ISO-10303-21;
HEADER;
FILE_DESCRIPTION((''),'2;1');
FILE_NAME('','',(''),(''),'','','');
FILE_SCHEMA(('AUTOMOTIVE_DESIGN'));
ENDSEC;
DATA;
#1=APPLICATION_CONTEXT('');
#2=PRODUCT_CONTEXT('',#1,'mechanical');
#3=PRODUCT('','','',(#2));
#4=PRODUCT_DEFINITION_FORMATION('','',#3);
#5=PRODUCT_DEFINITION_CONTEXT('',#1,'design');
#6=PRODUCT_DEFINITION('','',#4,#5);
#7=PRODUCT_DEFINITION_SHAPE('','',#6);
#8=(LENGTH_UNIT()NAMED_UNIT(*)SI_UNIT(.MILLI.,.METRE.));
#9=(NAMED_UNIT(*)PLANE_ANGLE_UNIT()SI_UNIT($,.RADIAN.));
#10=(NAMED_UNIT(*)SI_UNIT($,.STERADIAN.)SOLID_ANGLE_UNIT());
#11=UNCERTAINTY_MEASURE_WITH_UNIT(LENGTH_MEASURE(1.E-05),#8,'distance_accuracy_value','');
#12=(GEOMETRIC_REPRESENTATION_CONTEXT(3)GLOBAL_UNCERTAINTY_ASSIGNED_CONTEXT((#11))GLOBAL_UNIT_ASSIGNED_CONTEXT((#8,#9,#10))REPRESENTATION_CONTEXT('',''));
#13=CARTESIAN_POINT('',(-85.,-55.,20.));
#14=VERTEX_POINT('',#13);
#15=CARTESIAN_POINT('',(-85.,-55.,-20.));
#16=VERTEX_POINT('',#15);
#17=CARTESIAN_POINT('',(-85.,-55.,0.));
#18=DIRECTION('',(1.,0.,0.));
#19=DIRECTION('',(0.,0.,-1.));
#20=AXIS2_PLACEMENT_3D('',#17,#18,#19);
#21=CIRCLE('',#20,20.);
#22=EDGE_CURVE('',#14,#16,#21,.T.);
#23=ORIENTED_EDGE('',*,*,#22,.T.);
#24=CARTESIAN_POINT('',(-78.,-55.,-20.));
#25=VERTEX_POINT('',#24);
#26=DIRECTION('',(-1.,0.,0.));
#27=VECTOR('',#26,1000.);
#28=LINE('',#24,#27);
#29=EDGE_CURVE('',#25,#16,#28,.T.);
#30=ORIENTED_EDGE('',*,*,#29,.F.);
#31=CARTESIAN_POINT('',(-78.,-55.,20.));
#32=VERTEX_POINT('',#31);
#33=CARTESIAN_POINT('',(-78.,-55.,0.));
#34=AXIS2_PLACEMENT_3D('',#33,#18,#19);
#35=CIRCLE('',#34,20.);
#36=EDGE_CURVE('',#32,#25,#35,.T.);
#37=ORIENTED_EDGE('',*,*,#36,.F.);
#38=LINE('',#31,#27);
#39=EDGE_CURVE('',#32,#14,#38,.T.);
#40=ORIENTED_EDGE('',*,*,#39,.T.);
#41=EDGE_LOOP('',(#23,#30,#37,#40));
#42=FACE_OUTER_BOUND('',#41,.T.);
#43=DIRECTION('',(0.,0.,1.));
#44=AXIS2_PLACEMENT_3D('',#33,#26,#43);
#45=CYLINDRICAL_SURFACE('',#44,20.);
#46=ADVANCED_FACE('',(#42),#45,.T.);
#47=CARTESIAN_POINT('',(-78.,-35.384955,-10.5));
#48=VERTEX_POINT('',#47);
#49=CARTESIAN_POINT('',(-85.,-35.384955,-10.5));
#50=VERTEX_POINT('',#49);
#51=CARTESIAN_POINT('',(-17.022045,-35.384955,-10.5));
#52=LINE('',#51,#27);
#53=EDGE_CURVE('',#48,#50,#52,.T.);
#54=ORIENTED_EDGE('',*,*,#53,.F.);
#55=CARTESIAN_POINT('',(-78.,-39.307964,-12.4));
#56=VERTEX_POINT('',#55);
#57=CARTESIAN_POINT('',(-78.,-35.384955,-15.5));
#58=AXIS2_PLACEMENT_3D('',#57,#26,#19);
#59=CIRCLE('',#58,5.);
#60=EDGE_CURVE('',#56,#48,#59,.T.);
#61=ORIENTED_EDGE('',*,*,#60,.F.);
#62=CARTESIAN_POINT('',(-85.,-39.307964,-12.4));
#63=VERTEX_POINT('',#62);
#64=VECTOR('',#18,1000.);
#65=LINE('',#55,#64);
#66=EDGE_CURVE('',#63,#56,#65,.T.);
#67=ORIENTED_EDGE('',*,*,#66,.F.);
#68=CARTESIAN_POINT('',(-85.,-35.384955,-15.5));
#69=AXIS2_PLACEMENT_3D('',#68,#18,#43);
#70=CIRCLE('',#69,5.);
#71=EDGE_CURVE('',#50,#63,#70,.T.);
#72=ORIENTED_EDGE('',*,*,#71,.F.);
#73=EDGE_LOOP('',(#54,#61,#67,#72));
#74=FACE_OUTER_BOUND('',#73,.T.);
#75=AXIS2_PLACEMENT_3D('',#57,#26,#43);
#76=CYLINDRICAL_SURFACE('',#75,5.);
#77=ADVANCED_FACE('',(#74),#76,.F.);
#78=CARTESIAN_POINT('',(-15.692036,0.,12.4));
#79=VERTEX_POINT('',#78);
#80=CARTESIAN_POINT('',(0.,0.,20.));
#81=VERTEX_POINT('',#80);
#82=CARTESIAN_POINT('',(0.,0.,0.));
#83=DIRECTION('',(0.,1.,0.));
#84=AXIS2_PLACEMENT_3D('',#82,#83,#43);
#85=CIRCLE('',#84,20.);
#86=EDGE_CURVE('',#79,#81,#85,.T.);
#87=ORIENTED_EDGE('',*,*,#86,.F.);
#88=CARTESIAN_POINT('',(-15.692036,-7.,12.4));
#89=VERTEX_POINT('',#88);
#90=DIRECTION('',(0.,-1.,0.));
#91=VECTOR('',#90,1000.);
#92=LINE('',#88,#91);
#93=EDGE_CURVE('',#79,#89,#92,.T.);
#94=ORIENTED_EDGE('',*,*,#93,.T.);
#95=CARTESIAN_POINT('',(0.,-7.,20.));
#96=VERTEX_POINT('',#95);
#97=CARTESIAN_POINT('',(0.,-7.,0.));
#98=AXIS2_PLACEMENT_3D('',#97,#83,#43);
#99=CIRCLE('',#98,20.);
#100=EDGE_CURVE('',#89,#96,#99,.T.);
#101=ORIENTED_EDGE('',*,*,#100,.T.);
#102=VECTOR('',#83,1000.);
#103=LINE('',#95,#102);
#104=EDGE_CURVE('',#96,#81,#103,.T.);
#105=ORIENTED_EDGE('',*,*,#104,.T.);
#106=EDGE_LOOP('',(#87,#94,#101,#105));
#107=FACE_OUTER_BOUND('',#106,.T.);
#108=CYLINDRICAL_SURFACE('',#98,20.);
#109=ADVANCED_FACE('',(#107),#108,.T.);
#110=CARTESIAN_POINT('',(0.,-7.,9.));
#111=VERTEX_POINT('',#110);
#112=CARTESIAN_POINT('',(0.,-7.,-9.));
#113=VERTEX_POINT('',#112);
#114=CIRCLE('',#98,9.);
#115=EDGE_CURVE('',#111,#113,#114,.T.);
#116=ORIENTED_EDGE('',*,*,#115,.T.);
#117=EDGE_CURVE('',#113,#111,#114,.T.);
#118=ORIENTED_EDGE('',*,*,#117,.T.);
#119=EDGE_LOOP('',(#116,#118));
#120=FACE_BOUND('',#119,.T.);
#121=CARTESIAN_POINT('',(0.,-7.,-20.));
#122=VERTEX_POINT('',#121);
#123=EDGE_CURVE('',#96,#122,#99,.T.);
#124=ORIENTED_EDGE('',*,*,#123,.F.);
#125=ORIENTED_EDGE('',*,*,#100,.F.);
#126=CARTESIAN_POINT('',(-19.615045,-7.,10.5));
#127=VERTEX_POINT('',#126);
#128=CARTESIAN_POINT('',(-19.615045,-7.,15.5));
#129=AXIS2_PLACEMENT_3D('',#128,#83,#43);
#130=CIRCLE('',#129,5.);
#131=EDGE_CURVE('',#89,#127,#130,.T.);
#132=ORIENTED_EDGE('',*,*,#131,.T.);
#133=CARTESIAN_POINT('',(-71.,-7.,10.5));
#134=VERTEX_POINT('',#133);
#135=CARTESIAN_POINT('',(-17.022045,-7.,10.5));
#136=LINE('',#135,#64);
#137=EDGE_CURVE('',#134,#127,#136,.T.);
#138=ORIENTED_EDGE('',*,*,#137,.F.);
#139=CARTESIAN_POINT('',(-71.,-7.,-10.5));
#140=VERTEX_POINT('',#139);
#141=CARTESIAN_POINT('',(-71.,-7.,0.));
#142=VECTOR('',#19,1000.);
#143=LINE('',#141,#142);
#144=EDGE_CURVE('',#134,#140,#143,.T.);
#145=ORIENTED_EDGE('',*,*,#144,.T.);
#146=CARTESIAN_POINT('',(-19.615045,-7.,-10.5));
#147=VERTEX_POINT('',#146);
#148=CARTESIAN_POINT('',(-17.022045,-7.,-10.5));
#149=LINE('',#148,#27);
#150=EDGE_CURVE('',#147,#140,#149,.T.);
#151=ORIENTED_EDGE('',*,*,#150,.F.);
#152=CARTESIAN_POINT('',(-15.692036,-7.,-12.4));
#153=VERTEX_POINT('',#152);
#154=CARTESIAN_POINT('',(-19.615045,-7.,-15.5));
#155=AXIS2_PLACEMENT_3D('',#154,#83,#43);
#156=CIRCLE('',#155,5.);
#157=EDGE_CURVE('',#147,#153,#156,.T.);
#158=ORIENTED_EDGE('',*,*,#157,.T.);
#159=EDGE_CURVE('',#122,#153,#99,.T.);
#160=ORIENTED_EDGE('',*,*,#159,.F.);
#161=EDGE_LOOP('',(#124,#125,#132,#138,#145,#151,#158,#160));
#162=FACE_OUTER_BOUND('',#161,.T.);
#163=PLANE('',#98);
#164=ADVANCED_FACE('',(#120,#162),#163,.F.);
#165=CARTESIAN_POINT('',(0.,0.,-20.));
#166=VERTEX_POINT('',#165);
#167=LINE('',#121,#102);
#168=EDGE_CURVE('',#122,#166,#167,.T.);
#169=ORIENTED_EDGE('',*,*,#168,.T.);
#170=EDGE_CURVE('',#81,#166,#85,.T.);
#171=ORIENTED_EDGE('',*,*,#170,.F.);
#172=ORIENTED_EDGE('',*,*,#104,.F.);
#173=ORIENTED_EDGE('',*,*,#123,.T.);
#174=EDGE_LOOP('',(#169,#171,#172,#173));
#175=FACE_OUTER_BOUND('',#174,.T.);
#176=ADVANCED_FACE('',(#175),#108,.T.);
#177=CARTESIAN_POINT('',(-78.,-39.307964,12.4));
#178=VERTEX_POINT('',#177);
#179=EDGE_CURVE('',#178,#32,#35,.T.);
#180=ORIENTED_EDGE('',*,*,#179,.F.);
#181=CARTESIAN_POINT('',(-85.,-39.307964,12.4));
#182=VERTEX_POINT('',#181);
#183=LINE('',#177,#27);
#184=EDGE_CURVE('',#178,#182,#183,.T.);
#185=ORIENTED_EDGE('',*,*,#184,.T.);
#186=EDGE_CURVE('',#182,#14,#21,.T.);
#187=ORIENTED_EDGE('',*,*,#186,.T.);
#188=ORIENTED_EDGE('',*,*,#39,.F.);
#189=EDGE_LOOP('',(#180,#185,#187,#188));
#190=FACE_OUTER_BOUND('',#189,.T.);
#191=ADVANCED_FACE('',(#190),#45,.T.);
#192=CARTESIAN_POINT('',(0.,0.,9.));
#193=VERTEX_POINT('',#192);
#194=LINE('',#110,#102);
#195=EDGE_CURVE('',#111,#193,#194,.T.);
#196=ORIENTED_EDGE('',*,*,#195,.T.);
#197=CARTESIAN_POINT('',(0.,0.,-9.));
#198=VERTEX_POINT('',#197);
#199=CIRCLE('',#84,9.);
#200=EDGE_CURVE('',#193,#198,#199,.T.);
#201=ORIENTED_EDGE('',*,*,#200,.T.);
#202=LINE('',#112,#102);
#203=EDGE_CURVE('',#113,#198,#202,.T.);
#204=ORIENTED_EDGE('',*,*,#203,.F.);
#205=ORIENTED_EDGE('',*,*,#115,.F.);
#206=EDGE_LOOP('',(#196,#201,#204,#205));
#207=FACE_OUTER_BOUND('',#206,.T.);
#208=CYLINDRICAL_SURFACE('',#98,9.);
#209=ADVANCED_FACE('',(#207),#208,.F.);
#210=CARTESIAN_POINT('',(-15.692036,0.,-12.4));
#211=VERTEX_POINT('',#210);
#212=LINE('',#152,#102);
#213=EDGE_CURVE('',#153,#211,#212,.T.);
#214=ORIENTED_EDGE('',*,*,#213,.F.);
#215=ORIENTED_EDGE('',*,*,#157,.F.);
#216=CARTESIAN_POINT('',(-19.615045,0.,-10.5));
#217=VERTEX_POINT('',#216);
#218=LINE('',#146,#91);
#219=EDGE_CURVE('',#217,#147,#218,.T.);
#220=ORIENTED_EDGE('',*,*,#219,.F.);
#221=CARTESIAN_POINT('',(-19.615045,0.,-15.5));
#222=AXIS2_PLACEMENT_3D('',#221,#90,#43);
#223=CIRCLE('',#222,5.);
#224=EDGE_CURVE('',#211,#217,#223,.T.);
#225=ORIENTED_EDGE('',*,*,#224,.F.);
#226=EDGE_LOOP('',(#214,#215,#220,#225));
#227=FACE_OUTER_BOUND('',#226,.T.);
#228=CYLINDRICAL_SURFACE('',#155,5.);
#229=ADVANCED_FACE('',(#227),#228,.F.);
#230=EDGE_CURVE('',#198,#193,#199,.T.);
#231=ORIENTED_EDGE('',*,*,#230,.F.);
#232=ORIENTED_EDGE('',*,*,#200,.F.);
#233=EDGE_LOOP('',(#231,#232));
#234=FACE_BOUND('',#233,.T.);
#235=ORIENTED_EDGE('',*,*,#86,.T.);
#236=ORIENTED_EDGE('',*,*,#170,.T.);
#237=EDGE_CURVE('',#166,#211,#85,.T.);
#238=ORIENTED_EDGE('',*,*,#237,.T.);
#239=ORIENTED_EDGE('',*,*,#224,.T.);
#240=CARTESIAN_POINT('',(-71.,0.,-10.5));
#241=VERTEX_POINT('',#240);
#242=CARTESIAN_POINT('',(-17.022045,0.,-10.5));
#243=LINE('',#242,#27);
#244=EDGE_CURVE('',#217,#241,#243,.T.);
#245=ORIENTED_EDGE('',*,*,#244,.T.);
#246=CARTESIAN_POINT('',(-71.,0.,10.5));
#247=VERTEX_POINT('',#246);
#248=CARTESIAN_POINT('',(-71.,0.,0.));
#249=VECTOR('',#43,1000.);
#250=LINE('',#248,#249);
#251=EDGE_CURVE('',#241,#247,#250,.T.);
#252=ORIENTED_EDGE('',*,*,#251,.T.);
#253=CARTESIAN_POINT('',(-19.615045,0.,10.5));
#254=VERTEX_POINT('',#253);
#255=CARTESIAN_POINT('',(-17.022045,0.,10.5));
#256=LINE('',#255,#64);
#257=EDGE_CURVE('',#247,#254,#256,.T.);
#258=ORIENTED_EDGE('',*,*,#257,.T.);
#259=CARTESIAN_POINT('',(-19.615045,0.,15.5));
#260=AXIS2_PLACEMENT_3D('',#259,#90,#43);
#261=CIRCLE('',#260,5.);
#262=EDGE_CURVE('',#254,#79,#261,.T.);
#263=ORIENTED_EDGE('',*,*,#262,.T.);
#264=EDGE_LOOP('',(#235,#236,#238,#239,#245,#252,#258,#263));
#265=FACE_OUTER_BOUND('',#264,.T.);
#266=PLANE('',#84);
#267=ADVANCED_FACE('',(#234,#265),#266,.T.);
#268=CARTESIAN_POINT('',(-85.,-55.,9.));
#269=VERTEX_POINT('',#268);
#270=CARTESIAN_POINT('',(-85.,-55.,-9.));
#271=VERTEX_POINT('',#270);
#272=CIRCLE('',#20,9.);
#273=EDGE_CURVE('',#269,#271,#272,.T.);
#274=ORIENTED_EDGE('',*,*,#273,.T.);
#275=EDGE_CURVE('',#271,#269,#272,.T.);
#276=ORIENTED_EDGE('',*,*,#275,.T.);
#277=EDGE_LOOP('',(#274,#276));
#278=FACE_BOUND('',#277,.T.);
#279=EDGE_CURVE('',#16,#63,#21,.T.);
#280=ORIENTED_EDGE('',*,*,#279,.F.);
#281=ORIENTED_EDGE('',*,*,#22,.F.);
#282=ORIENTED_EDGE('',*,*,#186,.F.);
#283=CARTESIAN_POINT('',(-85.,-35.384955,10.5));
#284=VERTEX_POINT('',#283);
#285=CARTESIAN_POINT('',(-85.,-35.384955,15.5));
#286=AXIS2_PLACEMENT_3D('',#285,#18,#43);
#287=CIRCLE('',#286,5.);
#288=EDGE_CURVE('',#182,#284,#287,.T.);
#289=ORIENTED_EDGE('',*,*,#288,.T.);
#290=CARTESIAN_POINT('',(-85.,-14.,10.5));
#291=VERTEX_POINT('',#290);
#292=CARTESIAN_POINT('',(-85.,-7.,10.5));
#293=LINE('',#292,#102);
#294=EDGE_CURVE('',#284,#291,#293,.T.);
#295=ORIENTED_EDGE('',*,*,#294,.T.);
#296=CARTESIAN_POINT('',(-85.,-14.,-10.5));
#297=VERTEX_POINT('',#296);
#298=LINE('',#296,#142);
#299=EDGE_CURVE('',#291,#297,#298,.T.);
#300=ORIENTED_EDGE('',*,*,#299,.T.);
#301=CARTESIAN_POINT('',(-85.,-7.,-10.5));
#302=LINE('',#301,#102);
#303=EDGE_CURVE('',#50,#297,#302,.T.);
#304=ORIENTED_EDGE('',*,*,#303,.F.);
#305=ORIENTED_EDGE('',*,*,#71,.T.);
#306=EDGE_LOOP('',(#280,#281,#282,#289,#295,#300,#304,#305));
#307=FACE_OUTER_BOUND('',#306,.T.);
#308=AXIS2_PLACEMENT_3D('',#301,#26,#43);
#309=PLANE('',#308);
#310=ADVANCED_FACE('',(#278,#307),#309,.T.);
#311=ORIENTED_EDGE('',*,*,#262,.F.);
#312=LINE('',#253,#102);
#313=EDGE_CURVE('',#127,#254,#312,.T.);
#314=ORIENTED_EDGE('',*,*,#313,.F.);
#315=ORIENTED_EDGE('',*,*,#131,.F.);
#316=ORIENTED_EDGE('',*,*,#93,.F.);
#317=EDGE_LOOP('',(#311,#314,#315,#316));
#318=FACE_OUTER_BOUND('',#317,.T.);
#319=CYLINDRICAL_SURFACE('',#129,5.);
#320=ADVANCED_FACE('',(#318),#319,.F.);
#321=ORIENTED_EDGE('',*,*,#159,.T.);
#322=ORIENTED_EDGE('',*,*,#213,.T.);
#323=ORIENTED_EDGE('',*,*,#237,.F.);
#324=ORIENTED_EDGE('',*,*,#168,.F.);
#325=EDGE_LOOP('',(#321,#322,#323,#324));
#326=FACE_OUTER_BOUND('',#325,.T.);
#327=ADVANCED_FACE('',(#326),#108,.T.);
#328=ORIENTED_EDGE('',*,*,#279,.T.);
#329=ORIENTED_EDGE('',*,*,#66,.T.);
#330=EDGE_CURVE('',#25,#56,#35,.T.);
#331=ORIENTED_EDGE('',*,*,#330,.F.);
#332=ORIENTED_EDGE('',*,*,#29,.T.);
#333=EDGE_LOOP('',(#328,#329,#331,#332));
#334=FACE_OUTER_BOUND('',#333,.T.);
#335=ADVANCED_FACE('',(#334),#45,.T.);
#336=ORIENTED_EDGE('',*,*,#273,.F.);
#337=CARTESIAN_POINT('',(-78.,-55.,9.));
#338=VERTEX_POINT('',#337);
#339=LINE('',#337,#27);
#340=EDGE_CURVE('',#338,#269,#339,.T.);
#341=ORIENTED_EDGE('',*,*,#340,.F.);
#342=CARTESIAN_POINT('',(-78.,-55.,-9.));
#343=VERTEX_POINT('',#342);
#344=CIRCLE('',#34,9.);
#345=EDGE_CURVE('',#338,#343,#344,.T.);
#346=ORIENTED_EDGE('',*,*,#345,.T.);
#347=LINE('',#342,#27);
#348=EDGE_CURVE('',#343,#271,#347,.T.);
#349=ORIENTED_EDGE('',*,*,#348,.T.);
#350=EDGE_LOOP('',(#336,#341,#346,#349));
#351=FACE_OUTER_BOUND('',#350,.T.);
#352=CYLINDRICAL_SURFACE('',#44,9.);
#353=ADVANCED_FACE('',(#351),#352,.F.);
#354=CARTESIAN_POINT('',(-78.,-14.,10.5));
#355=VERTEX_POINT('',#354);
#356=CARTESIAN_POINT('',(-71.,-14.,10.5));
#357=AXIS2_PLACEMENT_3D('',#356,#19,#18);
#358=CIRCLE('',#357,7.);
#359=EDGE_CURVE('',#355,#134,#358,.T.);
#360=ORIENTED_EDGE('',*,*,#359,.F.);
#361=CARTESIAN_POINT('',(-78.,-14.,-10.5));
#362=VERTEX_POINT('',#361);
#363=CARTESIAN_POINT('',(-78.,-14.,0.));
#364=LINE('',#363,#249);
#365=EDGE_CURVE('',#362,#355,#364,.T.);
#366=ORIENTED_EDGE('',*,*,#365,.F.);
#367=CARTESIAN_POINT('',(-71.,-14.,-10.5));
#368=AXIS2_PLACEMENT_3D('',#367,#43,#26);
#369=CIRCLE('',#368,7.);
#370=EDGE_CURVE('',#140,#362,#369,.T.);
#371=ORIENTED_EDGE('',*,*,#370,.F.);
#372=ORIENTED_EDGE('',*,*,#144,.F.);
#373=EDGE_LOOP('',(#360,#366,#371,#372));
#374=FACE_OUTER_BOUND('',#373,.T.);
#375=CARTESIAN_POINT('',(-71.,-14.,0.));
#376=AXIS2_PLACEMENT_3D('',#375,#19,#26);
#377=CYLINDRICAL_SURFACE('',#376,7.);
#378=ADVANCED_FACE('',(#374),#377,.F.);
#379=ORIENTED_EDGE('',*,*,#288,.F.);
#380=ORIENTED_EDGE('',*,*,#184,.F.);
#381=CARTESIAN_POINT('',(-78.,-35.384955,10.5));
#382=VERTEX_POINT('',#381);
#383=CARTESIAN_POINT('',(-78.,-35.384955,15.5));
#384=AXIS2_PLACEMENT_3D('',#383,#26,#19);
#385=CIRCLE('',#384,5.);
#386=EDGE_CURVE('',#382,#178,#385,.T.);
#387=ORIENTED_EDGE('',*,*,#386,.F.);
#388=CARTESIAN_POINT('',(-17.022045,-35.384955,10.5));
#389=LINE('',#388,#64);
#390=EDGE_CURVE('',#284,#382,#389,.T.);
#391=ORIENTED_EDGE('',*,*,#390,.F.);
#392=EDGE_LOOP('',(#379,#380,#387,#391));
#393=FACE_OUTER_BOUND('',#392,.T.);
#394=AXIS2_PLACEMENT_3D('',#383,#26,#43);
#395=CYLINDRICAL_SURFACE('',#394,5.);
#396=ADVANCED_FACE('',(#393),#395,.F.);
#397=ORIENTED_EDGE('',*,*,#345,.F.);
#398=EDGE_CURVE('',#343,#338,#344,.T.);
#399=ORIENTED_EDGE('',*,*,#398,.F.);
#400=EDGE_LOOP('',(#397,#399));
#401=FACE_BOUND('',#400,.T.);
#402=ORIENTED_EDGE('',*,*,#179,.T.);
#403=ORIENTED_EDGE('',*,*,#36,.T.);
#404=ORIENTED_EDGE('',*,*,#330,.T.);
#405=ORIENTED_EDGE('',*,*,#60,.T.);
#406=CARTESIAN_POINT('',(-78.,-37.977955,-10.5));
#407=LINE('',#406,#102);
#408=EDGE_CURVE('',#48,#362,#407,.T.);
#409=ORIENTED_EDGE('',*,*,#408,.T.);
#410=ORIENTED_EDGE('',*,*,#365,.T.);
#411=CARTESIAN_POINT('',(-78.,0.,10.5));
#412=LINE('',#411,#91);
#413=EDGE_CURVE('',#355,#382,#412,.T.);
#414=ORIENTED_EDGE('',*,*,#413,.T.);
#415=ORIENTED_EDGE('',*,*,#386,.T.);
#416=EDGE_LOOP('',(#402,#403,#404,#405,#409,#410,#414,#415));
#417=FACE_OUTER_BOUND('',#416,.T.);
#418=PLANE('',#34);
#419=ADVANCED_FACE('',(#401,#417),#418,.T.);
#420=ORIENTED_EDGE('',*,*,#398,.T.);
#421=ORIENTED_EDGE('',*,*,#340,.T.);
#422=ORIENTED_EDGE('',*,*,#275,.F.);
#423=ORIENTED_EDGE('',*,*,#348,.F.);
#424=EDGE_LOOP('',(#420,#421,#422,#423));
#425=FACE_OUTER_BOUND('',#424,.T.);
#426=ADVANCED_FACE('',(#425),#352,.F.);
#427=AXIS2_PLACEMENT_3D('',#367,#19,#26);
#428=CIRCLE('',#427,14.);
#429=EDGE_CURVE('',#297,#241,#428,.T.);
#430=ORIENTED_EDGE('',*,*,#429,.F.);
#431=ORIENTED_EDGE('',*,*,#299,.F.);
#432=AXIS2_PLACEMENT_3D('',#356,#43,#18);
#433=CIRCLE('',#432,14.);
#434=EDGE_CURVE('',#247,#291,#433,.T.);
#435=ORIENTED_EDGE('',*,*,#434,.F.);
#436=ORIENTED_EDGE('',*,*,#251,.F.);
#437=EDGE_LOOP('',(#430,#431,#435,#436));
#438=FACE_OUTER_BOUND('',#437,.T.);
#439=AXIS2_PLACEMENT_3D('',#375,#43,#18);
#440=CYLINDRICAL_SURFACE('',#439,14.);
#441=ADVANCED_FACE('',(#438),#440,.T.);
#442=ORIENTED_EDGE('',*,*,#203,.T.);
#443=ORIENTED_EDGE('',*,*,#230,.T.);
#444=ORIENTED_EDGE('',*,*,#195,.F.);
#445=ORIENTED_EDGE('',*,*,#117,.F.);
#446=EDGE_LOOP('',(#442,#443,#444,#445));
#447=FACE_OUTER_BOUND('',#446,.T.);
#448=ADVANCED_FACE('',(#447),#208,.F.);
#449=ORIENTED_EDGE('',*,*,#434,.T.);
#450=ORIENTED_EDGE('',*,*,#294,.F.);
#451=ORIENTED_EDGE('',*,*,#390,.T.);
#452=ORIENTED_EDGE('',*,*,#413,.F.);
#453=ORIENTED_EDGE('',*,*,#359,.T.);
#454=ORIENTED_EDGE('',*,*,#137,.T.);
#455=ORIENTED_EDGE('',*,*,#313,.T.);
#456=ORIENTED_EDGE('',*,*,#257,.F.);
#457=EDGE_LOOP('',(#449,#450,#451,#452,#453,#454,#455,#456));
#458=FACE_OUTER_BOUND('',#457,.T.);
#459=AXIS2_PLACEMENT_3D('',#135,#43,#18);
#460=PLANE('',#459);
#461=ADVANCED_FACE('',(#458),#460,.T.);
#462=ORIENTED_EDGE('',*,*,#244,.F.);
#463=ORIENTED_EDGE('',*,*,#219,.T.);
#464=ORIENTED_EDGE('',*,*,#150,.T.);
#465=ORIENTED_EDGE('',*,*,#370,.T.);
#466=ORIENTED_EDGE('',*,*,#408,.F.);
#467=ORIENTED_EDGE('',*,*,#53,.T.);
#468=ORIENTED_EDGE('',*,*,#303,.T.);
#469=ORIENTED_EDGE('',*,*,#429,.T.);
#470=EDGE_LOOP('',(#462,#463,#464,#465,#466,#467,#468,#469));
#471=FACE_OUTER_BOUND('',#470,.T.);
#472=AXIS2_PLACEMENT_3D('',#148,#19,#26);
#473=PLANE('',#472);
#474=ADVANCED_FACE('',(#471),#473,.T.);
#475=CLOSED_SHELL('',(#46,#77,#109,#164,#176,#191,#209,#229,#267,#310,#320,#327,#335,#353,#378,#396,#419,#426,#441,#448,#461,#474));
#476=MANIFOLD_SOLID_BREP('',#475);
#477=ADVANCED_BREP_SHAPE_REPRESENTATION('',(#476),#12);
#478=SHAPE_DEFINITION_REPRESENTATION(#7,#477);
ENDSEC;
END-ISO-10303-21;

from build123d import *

# Parameters (mm, degrees)
HORIZONTAL_ARM_PROFILE_R    = 9
HORIZONTAL_ARM_7MM_DEPTH    = 7
VERTICAL_ARM_PROFILE_R      = 9
VERTICAL_ARM_7MM_DEPTH      = 7
BEND_FILLET_R5_R            = 5
HORIZONTAL_ARM_FILLET_R14_R = 14
BEND_FILLET_R7_R            = 7


with BuildPart() as part:
    # Horizontal Arm Profile → Horizontal Arm 7mm (new body)
    with BuildSketch(Plane(origin=(0, 0, 0), x_dir=(1, 0, 0), z_dir=(0, 1, 0))):
        with BuildLine():
            Line((-17.022044531, 10.5), (-85, 10.5))
            Line((-85, 10.5), (-85, -10.5))
            Line((-85, -10.5), (-17.022044531, -10.5))
            ThreePointArc((-17.022044531, -10.5), (20, 0), (-17.022044531, 10.5))
        make_face()
        with Locations(Location((0, 0, 0), (0, 0, 270))):
            Circle(HORIZONTAL_ARM_PROFILE_R, mode=Mode.SUBTRACT)
    extrude(amount=-HORIZONTAL_ARM_7MM_DEPTH)

    # Vertical Arm Profile → Vertical Arm 7mm (add)
    with BuildSketch(Plane(origin=(-85, 0, 0), x_dir=(0, 0, -1), z_dir=(1, 0, 0))):
        with BuildLine():
            Line((-10.5, 0), (-10.5, -37.977955469))
            ThreePointArc((-10.5, -37.977955469), (0, -75), (10.5, -37.977955469))
            Line((10.5, -37.977955469), (10.5, 0))
            Line((10.5, 0), (-10.5, 0))
        make_face()
        with Locations((0, -55)):
            Circle(VERTICAL_ARM_PROFILE_R, mode=Mode.SUBTRACT)
    extrude(amount=VERTICAL_ARM_7MM_DEPTH)

    # Bend Fillet R5
    bend_fillet_r5_edges = [part.edges().sort_by_distance(p)[0] for p in [
        (-81.5, -37.977955469, -10.5),
        (-81.5, -37.977955469, 10.5),
        (-17.022044531, -3.5, 10.5),
        (-17.022044531, -3.5, -10.5),
    ]]
    fillet(bend_fillet_r5_edges, radius=BEND_FILLET_R5_R)

    # Horizontal Arm Fillet R14
    horizontal_arm_fillet_r14_edges = [part.edges().sort_by_distance(p)[0] for p in [
        (-85, 0, 0),
    ]]
    fillet(horizontal_arm_fillet_r14_edges, radius=HORIZONTAL_ARM_FILLET_R14_R)

    # Bend Fillet R7
    bend_fillet_r7_edges = [part.edges().sort_by_distance(p)[0] for p in [
        (-78, -7, 0),
    ]]
    fillet(bend_fillet_r7_edges, radius=BEND_FILLET_R7_R)


solid = part.part
